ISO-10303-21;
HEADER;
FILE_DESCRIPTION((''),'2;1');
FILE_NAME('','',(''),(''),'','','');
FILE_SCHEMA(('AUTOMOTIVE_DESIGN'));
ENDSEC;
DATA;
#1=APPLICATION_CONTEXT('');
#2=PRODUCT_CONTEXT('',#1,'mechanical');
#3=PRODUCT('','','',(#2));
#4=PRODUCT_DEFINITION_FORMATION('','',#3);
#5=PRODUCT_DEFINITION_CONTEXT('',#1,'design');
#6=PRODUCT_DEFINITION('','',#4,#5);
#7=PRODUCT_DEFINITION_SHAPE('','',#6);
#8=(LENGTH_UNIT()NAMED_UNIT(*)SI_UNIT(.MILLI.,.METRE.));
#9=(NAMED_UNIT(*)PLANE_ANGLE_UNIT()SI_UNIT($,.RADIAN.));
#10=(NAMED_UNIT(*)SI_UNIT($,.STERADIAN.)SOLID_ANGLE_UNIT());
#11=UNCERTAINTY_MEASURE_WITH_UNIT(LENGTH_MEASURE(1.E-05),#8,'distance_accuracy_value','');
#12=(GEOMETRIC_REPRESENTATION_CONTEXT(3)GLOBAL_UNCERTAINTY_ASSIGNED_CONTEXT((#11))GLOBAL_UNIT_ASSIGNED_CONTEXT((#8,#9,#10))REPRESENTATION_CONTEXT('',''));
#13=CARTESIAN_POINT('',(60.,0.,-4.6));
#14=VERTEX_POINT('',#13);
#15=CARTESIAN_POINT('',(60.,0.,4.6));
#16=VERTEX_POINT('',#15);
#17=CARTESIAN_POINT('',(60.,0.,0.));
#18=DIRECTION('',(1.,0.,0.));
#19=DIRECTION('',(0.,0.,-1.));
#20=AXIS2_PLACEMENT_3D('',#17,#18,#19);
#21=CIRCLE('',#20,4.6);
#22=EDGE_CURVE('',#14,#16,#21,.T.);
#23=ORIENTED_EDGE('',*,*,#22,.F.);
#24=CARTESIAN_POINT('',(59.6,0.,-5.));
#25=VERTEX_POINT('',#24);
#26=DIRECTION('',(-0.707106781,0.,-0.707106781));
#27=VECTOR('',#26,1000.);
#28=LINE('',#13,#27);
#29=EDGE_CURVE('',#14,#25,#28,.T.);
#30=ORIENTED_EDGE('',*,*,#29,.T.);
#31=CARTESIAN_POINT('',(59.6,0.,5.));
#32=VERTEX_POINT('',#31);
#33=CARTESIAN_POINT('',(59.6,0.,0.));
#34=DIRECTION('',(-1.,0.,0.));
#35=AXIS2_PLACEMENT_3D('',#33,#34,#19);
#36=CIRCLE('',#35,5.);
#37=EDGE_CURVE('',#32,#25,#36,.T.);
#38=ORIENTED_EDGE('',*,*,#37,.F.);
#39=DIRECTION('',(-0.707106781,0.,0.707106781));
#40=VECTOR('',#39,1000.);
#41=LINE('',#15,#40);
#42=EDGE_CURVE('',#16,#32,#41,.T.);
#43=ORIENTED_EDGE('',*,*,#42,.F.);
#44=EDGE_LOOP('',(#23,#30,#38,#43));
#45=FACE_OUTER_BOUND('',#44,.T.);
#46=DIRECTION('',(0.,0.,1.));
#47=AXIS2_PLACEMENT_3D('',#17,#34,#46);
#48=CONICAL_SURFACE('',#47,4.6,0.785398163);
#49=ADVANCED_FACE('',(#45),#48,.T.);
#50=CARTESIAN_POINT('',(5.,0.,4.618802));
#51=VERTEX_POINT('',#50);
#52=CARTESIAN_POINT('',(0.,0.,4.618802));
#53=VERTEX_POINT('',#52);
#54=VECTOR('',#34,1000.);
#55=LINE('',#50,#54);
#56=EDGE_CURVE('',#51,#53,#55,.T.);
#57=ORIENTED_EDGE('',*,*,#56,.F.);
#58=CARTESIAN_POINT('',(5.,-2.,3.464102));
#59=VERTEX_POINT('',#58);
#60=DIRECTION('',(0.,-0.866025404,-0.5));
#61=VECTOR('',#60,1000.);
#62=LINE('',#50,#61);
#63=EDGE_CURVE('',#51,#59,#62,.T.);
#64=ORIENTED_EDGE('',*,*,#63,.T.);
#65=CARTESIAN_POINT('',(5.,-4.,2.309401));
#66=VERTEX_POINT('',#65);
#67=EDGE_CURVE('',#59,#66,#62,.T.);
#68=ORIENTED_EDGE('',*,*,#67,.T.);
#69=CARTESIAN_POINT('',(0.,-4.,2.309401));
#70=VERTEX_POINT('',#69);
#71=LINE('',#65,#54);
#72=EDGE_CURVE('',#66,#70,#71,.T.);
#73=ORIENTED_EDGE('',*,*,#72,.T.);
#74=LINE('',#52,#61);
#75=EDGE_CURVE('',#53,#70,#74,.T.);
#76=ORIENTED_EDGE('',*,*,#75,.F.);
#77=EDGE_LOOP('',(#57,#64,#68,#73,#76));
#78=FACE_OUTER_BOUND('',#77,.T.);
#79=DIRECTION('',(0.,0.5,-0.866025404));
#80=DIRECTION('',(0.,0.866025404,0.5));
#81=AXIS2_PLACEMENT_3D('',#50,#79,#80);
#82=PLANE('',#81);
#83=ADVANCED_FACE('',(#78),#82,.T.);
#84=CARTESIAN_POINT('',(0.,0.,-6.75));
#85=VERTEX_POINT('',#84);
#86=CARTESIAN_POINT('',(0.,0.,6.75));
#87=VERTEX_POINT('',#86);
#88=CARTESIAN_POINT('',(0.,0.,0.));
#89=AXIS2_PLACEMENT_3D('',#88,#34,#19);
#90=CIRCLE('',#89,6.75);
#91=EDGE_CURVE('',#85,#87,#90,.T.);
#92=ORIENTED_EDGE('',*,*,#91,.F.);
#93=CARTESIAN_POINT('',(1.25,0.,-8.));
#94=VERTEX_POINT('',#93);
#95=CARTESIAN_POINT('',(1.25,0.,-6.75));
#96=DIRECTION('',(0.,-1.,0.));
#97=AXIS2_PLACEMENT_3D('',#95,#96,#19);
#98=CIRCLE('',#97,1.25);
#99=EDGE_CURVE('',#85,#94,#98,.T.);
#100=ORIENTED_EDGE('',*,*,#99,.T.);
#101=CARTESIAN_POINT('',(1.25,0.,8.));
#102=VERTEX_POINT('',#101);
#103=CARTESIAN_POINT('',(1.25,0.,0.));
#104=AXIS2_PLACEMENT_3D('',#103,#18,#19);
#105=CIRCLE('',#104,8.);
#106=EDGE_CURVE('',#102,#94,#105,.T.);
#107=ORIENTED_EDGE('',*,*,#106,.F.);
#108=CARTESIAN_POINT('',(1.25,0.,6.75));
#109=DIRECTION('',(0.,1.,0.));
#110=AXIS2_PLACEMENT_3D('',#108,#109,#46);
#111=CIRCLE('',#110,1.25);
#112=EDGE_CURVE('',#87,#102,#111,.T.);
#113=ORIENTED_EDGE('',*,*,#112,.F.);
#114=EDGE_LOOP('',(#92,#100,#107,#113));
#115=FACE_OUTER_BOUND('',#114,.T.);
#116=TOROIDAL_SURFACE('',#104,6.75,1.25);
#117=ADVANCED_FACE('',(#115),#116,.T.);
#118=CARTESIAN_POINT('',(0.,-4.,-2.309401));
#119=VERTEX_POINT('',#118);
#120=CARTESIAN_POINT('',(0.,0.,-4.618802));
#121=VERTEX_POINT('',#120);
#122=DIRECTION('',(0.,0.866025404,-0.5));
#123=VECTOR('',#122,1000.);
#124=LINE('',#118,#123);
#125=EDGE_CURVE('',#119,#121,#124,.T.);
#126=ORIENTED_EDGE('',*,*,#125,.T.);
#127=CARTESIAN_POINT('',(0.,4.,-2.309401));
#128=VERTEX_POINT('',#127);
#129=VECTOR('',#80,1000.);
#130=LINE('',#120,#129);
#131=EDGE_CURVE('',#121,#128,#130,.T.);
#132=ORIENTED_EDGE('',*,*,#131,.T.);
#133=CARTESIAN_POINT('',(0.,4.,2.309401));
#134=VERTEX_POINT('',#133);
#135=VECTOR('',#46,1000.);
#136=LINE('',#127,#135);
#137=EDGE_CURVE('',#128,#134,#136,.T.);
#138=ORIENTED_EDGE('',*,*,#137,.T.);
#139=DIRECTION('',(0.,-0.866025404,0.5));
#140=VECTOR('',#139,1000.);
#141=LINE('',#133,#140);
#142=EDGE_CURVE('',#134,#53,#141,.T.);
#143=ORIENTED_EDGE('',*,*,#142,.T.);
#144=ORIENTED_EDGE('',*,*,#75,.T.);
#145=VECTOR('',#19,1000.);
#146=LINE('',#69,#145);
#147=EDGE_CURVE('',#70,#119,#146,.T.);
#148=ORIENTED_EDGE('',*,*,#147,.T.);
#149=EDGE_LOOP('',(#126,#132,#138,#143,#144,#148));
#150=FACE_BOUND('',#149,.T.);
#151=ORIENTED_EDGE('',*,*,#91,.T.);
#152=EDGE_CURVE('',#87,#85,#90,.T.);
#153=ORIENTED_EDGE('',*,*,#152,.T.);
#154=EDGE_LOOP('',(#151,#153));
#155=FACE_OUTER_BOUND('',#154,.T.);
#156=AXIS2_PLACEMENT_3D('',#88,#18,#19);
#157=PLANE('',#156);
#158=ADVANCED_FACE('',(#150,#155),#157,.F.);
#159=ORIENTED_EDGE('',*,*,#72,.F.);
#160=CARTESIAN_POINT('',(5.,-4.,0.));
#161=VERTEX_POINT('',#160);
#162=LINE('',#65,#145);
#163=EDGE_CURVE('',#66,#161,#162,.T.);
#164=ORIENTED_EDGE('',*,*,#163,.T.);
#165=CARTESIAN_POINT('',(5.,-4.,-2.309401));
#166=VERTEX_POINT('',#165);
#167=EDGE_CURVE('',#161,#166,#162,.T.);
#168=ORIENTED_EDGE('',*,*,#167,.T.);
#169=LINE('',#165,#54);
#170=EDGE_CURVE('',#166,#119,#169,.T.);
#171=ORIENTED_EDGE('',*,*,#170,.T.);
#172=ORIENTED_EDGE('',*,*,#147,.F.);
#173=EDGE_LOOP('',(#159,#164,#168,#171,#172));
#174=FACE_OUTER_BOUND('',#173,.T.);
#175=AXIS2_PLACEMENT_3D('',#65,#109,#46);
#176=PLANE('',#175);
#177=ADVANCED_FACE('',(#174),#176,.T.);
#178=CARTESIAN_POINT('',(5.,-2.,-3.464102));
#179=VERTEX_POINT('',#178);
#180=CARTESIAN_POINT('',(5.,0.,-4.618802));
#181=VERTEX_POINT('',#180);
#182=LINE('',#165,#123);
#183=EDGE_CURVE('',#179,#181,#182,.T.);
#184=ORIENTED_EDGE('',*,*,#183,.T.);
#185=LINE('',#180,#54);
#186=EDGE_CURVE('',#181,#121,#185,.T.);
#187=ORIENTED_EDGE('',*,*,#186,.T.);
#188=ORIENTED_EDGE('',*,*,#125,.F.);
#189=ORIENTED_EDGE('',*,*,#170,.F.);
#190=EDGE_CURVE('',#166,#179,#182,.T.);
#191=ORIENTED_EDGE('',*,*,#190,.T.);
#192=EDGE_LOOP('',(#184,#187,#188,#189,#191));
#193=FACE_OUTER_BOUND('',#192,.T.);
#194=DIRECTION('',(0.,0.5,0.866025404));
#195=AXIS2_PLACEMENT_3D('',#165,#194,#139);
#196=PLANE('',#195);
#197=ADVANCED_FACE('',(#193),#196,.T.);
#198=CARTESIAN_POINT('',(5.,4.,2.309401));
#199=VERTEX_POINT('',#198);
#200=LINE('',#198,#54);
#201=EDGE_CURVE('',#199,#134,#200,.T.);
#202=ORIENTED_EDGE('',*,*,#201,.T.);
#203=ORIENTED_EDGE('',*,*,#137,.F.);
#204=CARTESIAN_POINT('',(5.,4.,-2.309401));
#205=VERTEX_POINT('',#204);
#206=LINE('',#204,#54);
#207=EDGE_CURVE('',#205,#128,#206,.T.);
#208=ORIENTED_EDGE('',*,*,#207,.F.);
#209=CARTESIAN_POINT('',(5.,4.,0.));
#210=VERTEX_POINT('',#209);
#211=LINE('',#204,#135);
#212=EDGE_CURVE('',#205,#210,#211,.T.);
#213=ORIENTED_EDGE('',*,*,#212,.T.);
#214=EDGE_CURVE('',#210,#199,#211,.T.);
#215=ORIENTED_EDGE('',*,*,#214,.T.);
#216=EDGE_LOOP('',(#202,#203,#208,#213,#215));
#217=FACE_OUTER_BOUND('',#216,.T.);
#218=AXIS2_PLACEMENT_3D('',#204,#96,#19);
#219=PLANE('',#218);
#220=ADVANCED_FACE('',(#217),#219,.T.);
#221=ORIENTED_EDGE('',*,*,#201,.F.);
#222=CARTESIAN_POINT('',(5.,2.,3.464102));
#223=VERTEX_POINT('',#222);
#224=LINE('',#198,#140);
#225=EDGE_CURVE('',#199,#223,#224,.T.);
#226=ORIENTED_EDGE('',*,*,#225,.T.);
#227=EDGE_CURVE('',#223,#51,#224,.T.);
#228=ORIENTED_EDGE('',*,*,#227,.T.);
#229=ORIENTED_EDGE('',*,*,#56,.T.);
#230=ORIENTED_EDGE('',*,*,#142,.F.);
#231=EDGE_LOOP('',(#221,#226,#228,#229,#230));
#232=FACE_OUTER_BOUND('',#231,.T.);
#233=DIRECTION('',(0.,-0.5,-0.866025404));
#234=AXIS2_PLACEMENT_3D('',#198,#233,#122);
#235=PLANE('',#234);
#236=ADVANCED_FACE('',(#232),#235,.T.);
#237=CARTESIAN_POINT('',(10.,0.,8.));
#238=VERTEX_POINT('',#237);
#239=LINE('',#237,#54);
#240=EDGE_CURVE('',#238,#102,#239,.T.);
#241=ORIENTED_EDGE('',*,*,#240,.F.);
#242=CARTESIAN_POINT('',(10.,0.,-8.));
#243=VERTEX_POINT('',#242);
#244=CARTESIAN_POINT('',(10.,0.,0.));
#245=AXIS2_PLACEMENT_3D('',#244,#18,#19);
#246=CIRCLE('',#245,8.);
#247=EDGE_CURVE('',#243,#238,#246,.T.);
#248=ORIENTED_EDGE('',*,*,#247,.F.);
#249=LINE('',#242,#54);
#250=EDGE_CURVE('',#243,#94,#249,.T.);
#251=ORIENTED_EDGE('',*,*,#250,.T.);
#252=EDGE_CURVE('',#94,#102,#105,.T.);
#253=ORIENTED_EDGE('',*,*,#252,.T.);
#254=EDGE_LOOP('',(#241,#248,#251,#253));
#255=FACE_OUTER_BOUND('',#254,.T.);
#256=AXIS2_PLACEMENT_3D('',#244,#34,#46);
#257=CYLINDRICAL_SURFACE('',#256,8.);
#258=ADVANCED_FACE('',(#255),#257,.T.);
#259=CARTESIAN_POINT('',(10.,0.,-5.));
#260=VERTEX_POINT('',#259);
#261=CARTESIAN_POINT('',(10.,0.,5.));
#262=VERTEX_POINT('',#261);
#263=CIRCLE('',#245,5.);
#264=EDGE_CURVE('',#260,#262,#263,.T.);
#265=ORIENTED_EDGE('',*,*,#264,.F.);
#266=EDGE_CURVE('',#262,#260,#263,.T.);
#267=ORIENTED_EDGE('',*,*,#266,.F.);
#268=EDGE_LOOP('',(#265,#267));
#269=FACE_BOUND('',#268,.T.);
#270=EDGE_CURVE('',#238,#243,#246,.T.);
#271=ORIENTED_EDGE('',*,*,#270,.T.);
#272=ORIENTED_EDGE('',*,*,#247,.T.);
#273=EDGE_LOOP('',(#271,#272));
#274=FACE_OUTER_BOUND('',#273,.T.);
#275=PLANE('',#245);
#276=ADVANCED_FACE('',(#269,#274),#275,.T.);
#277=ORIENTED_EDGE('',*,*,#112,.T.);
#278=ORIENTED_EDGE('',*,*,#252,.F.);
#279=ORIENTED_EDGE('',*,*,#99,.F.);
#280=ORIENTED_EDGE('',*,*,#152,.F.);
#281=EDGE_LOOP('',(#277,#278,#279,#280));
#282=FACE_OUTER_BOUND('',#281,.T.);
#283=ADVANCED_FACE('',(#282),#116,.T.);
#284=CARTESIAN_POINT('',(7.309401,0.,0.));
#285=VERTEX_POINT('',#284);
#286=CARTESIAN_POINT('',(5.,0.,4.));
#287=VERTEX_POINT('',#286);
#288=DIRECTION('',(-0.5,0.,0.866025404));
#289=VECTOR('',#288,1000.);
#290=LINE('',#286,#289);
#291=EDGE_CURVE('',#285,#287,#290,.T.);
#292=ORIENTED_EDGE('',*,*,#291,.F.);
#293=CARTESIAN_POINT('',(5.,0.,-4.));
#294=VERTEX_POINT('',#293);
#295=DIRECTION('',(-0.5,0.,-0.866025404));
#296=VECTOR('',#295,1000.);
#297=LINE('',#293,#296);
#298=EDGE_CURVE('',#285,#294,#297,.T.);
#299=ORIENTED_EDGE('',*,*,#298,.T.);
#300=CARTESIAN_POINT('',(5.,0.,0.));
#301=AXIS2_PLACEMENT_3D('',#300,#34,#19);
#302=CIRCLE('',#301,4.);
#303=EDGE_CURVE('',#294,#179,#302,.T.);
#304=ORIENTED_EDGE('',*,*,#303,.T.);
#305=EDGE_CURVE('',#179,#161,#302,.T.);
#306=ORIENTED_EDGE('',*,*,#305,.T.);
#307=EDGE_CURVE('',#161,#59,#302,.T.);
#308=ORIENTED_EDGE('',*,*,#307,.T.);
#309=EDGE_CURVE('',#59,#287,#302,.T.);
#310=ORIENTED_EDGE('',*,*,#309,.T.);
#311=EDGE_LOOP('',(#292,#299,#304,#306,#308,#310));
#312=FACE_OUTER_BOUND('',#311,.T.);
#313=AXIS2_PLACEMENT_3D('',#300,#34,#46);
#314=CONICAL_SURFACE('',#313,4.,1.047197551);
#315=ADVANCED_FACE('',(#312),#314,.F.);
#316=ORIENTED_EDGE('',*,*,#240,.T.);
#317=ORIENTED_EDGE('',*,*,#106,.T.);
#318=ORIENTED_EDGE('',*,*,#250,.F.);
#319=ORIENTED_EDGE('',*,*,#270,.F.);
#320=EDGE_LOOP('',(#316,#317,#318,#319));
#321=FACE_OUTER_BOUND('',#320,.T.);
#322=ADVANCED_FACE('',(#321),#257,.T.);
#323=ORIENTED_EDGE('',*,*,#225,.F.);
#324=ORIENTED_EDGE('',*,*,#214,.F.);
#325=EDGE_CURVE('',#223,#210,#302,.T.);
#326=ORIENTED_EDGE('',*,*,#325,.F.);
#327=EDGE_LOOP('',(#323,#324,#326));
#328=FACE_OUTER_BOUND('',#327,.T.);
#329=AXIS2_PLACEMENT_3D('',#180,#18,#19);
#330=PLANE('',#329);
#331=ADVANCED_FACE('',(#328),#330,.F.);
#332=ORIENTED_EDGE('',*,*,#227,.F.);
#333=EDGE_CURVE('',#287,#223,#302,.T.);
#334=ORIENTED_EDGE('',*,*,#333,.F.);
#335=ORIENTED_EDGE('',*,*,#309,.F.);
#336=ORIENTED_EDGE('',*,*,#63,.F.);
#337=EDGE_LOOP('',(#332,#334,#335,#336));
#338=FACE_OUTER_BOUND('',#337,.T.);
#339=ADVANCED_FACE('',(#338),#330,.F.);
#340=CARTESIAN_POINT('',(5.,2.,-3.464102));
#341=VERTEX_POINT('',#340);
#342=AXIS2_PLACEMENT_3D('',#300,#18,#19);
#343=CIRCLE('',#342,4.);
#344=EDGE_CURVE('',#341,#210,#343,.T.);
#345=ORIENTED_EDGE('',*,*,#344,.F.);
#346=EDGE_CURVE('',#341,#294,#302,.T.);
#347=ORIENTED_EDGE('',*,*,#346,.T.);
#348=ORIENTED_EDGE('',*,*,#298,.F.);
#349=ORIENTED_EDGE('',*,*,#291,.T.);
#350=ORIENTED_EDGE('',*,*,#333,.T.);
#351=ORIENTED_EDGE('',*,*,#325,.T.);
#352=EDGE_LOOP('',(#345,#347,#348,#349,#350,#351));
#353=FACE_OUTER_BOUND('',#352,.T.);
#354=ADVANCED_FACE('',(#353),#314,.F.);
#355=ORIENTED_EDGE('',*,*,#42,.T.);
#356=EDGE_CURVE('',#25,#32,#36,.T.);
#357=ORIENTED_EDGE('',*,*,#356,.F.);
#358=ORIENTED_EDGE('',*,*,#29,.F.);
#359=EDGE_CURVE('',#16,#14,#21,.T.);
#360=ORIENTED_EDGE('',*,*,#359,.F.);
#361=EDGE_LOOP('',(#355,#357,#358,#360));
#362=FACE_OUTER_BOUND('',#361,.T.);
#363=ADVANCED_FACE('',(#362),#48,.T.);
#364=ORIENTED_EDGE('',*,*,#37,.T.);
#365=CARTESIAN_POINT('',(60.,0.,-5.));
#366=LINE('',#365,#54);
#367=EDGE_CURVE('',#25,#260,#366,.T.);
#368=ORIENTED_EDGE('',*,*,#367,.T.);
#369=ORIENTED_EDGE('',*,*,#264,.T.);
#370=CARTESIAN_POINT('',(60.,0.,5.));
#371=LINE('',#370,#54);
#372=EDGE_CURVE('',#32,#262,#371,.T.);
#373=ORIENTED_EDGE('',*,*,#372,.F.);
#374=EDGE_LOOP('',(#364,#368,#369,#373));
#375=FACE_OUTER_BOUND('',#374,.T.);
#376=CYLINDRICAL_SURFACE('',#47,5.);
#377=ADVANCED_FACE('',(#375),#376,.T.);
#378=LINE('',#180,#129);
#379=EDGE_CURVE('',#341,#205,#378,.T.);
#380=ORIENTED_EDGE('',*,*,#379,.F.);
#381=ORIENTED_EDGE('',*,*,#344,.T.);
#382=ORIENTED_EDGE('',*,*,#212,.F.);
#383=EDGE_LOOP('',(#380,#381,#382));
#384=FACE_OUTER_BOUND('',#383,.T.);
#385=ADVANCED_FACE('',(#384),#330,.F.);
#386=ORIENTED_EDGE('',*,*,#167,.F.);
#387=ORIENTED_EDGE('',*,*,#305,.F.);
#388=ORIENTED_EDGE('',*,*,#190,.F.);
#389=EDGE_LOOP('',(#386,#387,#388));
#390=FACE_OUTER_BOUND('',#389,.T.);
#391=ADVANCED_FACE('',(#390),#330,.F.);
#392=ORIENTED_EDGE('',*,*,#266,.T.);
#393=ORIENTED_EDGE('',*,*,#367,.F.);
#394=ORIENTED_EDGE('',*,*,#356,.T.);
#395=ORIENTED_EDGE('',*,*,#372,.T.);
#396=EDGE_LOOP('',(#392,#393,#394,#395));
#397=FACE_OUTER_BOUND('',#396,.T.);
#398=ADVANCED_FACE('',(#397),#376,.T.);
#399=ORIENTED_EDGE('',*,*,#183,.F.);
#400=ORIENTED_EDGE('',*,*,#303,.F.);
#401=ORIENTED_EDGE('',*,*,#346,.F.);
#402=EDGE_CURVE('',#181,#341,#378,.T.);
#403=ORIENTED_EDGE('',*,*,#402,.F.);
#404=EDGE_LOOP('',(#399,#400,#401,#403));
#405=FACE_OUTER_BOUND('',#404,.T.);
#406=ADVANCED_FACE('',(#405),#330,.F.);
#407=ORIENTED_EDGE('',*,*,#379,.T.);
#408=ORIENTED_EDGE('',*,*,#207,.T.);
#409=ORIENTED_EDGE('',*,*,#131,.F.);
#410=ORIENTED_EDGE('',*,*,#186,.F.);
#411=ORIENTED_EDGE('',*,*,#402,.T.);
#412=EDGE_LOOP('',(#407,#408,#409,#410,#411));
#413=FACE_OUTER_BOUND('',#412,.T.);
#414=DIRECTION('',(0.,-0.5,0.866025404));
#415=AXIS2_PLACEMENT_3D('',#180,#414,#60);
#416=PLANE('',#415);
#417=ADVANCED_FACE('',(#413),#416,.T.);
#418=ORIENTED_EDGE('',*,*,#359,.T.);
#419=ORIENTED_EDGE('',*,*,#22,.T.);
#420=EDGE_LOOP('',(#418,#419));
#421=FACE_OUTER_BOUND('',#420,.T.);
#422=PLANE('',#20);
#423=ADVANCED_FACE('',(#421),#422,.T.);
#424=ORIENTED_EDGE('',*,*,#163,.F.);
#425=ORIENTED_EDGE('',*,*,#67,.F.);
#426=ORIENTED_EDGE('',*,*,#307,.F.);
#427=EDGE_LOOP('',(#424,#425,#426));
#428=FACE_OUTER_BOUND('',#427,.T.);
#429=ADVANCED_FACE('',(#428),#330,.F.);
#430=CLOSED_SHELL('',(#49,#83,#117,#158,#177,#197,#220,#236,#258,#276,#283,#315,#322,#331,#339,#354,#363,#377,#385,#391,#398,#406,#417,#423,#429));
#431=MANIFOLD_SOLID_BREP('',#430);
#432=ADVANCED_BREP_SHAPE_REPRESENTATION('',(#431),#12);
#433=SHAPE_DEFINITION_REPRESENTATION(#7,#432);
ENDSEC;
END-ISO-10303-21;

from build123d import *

# Parameters (mm, degrees)
SKETCH1_R           = 8
BASEHEAD_DEPTH      = 10
SKETCH2_R           = 5
BASEBODY_DEPTH      = 50
HEXAGONSOCKET_DEPTH = 5
TOPFILLET_R         = 1.25
CHAMFER1_SIZE       = 0.4


with BuildPart() as part:
    # Sketch1 → BaseHead (new body)
    with BuildSketch(Plane(origin=(0, 0, 0), x_dir=(0, 0, -1), z_dir=(1, 0, 0))):
        Circle(SKETCH1_R)
    extrude(amount=BASEHEAD_DEPTH)

    # Sketch2 → BaseBody (add)
    with BuildSketch(Plane(origin=(10, 0, 0), x_dir=(0, 0, -1), z_dir=(1, 0, 0))):
        Circle(SKETCH2_R)
    extrude(amount=BASEBODY_DEPTH)

    # Sketch3 → HexagonSocket (cut)
    with BuildSketch(Plane(origin=(0, 0, 0), x_dir=(0, 0, -1), z_dir=(1, 0, 0))):
        Polygon((4.618802154, 0), (2.309401077, 4), (-2.309401077, 4), (-4.618802154, 0), (-2.309401077, -4), (2.309401077, -4), align=None)
    extrude(amount=HEXAGONSOCKET_DEPTH, mode=Mode.SUBTRACT)

    # Sketch4 → Cut-Revolve1 (revolve, cut)
    with BuildSketch(Plane(origin=(-4.19613823, 0.75, 0), x_dir=(-1, 0, 0), z_dir=(0, 0, 1)), mode=Mode.PRIVATE) as cut_revolve1_sk:
        Polygon((-9.19613823, 4.75), (-11.505539306, 0.75), (-9.19613823, 0.75), align=None)
    revolve(cut_revolve1_sk.sketch.rotate(Axis((0.838992387, 0, 0), (-1, 0, 0)), 90), axis=Axis((0.838992387, 0, 0), (-1, 0, 0)), mode=Mode.SUBTRACT)

    # TopFillet
    topfillet_edges = [part.edges().sort_by_distance(p)[0] for p in [
        (0, 0, 8),
    ]]
    fillet(topfillet_edges, radius=TOPFILLET_R)

    # Chamfer1
    chamfer1_edges = [part.edges().sort_by_distance(p)[0] for p in [
        (60, 0, 5),
    ]]
    chamfer(chamfer1_edges, length=CHAMFER1_SIZE)


solid = part.part
